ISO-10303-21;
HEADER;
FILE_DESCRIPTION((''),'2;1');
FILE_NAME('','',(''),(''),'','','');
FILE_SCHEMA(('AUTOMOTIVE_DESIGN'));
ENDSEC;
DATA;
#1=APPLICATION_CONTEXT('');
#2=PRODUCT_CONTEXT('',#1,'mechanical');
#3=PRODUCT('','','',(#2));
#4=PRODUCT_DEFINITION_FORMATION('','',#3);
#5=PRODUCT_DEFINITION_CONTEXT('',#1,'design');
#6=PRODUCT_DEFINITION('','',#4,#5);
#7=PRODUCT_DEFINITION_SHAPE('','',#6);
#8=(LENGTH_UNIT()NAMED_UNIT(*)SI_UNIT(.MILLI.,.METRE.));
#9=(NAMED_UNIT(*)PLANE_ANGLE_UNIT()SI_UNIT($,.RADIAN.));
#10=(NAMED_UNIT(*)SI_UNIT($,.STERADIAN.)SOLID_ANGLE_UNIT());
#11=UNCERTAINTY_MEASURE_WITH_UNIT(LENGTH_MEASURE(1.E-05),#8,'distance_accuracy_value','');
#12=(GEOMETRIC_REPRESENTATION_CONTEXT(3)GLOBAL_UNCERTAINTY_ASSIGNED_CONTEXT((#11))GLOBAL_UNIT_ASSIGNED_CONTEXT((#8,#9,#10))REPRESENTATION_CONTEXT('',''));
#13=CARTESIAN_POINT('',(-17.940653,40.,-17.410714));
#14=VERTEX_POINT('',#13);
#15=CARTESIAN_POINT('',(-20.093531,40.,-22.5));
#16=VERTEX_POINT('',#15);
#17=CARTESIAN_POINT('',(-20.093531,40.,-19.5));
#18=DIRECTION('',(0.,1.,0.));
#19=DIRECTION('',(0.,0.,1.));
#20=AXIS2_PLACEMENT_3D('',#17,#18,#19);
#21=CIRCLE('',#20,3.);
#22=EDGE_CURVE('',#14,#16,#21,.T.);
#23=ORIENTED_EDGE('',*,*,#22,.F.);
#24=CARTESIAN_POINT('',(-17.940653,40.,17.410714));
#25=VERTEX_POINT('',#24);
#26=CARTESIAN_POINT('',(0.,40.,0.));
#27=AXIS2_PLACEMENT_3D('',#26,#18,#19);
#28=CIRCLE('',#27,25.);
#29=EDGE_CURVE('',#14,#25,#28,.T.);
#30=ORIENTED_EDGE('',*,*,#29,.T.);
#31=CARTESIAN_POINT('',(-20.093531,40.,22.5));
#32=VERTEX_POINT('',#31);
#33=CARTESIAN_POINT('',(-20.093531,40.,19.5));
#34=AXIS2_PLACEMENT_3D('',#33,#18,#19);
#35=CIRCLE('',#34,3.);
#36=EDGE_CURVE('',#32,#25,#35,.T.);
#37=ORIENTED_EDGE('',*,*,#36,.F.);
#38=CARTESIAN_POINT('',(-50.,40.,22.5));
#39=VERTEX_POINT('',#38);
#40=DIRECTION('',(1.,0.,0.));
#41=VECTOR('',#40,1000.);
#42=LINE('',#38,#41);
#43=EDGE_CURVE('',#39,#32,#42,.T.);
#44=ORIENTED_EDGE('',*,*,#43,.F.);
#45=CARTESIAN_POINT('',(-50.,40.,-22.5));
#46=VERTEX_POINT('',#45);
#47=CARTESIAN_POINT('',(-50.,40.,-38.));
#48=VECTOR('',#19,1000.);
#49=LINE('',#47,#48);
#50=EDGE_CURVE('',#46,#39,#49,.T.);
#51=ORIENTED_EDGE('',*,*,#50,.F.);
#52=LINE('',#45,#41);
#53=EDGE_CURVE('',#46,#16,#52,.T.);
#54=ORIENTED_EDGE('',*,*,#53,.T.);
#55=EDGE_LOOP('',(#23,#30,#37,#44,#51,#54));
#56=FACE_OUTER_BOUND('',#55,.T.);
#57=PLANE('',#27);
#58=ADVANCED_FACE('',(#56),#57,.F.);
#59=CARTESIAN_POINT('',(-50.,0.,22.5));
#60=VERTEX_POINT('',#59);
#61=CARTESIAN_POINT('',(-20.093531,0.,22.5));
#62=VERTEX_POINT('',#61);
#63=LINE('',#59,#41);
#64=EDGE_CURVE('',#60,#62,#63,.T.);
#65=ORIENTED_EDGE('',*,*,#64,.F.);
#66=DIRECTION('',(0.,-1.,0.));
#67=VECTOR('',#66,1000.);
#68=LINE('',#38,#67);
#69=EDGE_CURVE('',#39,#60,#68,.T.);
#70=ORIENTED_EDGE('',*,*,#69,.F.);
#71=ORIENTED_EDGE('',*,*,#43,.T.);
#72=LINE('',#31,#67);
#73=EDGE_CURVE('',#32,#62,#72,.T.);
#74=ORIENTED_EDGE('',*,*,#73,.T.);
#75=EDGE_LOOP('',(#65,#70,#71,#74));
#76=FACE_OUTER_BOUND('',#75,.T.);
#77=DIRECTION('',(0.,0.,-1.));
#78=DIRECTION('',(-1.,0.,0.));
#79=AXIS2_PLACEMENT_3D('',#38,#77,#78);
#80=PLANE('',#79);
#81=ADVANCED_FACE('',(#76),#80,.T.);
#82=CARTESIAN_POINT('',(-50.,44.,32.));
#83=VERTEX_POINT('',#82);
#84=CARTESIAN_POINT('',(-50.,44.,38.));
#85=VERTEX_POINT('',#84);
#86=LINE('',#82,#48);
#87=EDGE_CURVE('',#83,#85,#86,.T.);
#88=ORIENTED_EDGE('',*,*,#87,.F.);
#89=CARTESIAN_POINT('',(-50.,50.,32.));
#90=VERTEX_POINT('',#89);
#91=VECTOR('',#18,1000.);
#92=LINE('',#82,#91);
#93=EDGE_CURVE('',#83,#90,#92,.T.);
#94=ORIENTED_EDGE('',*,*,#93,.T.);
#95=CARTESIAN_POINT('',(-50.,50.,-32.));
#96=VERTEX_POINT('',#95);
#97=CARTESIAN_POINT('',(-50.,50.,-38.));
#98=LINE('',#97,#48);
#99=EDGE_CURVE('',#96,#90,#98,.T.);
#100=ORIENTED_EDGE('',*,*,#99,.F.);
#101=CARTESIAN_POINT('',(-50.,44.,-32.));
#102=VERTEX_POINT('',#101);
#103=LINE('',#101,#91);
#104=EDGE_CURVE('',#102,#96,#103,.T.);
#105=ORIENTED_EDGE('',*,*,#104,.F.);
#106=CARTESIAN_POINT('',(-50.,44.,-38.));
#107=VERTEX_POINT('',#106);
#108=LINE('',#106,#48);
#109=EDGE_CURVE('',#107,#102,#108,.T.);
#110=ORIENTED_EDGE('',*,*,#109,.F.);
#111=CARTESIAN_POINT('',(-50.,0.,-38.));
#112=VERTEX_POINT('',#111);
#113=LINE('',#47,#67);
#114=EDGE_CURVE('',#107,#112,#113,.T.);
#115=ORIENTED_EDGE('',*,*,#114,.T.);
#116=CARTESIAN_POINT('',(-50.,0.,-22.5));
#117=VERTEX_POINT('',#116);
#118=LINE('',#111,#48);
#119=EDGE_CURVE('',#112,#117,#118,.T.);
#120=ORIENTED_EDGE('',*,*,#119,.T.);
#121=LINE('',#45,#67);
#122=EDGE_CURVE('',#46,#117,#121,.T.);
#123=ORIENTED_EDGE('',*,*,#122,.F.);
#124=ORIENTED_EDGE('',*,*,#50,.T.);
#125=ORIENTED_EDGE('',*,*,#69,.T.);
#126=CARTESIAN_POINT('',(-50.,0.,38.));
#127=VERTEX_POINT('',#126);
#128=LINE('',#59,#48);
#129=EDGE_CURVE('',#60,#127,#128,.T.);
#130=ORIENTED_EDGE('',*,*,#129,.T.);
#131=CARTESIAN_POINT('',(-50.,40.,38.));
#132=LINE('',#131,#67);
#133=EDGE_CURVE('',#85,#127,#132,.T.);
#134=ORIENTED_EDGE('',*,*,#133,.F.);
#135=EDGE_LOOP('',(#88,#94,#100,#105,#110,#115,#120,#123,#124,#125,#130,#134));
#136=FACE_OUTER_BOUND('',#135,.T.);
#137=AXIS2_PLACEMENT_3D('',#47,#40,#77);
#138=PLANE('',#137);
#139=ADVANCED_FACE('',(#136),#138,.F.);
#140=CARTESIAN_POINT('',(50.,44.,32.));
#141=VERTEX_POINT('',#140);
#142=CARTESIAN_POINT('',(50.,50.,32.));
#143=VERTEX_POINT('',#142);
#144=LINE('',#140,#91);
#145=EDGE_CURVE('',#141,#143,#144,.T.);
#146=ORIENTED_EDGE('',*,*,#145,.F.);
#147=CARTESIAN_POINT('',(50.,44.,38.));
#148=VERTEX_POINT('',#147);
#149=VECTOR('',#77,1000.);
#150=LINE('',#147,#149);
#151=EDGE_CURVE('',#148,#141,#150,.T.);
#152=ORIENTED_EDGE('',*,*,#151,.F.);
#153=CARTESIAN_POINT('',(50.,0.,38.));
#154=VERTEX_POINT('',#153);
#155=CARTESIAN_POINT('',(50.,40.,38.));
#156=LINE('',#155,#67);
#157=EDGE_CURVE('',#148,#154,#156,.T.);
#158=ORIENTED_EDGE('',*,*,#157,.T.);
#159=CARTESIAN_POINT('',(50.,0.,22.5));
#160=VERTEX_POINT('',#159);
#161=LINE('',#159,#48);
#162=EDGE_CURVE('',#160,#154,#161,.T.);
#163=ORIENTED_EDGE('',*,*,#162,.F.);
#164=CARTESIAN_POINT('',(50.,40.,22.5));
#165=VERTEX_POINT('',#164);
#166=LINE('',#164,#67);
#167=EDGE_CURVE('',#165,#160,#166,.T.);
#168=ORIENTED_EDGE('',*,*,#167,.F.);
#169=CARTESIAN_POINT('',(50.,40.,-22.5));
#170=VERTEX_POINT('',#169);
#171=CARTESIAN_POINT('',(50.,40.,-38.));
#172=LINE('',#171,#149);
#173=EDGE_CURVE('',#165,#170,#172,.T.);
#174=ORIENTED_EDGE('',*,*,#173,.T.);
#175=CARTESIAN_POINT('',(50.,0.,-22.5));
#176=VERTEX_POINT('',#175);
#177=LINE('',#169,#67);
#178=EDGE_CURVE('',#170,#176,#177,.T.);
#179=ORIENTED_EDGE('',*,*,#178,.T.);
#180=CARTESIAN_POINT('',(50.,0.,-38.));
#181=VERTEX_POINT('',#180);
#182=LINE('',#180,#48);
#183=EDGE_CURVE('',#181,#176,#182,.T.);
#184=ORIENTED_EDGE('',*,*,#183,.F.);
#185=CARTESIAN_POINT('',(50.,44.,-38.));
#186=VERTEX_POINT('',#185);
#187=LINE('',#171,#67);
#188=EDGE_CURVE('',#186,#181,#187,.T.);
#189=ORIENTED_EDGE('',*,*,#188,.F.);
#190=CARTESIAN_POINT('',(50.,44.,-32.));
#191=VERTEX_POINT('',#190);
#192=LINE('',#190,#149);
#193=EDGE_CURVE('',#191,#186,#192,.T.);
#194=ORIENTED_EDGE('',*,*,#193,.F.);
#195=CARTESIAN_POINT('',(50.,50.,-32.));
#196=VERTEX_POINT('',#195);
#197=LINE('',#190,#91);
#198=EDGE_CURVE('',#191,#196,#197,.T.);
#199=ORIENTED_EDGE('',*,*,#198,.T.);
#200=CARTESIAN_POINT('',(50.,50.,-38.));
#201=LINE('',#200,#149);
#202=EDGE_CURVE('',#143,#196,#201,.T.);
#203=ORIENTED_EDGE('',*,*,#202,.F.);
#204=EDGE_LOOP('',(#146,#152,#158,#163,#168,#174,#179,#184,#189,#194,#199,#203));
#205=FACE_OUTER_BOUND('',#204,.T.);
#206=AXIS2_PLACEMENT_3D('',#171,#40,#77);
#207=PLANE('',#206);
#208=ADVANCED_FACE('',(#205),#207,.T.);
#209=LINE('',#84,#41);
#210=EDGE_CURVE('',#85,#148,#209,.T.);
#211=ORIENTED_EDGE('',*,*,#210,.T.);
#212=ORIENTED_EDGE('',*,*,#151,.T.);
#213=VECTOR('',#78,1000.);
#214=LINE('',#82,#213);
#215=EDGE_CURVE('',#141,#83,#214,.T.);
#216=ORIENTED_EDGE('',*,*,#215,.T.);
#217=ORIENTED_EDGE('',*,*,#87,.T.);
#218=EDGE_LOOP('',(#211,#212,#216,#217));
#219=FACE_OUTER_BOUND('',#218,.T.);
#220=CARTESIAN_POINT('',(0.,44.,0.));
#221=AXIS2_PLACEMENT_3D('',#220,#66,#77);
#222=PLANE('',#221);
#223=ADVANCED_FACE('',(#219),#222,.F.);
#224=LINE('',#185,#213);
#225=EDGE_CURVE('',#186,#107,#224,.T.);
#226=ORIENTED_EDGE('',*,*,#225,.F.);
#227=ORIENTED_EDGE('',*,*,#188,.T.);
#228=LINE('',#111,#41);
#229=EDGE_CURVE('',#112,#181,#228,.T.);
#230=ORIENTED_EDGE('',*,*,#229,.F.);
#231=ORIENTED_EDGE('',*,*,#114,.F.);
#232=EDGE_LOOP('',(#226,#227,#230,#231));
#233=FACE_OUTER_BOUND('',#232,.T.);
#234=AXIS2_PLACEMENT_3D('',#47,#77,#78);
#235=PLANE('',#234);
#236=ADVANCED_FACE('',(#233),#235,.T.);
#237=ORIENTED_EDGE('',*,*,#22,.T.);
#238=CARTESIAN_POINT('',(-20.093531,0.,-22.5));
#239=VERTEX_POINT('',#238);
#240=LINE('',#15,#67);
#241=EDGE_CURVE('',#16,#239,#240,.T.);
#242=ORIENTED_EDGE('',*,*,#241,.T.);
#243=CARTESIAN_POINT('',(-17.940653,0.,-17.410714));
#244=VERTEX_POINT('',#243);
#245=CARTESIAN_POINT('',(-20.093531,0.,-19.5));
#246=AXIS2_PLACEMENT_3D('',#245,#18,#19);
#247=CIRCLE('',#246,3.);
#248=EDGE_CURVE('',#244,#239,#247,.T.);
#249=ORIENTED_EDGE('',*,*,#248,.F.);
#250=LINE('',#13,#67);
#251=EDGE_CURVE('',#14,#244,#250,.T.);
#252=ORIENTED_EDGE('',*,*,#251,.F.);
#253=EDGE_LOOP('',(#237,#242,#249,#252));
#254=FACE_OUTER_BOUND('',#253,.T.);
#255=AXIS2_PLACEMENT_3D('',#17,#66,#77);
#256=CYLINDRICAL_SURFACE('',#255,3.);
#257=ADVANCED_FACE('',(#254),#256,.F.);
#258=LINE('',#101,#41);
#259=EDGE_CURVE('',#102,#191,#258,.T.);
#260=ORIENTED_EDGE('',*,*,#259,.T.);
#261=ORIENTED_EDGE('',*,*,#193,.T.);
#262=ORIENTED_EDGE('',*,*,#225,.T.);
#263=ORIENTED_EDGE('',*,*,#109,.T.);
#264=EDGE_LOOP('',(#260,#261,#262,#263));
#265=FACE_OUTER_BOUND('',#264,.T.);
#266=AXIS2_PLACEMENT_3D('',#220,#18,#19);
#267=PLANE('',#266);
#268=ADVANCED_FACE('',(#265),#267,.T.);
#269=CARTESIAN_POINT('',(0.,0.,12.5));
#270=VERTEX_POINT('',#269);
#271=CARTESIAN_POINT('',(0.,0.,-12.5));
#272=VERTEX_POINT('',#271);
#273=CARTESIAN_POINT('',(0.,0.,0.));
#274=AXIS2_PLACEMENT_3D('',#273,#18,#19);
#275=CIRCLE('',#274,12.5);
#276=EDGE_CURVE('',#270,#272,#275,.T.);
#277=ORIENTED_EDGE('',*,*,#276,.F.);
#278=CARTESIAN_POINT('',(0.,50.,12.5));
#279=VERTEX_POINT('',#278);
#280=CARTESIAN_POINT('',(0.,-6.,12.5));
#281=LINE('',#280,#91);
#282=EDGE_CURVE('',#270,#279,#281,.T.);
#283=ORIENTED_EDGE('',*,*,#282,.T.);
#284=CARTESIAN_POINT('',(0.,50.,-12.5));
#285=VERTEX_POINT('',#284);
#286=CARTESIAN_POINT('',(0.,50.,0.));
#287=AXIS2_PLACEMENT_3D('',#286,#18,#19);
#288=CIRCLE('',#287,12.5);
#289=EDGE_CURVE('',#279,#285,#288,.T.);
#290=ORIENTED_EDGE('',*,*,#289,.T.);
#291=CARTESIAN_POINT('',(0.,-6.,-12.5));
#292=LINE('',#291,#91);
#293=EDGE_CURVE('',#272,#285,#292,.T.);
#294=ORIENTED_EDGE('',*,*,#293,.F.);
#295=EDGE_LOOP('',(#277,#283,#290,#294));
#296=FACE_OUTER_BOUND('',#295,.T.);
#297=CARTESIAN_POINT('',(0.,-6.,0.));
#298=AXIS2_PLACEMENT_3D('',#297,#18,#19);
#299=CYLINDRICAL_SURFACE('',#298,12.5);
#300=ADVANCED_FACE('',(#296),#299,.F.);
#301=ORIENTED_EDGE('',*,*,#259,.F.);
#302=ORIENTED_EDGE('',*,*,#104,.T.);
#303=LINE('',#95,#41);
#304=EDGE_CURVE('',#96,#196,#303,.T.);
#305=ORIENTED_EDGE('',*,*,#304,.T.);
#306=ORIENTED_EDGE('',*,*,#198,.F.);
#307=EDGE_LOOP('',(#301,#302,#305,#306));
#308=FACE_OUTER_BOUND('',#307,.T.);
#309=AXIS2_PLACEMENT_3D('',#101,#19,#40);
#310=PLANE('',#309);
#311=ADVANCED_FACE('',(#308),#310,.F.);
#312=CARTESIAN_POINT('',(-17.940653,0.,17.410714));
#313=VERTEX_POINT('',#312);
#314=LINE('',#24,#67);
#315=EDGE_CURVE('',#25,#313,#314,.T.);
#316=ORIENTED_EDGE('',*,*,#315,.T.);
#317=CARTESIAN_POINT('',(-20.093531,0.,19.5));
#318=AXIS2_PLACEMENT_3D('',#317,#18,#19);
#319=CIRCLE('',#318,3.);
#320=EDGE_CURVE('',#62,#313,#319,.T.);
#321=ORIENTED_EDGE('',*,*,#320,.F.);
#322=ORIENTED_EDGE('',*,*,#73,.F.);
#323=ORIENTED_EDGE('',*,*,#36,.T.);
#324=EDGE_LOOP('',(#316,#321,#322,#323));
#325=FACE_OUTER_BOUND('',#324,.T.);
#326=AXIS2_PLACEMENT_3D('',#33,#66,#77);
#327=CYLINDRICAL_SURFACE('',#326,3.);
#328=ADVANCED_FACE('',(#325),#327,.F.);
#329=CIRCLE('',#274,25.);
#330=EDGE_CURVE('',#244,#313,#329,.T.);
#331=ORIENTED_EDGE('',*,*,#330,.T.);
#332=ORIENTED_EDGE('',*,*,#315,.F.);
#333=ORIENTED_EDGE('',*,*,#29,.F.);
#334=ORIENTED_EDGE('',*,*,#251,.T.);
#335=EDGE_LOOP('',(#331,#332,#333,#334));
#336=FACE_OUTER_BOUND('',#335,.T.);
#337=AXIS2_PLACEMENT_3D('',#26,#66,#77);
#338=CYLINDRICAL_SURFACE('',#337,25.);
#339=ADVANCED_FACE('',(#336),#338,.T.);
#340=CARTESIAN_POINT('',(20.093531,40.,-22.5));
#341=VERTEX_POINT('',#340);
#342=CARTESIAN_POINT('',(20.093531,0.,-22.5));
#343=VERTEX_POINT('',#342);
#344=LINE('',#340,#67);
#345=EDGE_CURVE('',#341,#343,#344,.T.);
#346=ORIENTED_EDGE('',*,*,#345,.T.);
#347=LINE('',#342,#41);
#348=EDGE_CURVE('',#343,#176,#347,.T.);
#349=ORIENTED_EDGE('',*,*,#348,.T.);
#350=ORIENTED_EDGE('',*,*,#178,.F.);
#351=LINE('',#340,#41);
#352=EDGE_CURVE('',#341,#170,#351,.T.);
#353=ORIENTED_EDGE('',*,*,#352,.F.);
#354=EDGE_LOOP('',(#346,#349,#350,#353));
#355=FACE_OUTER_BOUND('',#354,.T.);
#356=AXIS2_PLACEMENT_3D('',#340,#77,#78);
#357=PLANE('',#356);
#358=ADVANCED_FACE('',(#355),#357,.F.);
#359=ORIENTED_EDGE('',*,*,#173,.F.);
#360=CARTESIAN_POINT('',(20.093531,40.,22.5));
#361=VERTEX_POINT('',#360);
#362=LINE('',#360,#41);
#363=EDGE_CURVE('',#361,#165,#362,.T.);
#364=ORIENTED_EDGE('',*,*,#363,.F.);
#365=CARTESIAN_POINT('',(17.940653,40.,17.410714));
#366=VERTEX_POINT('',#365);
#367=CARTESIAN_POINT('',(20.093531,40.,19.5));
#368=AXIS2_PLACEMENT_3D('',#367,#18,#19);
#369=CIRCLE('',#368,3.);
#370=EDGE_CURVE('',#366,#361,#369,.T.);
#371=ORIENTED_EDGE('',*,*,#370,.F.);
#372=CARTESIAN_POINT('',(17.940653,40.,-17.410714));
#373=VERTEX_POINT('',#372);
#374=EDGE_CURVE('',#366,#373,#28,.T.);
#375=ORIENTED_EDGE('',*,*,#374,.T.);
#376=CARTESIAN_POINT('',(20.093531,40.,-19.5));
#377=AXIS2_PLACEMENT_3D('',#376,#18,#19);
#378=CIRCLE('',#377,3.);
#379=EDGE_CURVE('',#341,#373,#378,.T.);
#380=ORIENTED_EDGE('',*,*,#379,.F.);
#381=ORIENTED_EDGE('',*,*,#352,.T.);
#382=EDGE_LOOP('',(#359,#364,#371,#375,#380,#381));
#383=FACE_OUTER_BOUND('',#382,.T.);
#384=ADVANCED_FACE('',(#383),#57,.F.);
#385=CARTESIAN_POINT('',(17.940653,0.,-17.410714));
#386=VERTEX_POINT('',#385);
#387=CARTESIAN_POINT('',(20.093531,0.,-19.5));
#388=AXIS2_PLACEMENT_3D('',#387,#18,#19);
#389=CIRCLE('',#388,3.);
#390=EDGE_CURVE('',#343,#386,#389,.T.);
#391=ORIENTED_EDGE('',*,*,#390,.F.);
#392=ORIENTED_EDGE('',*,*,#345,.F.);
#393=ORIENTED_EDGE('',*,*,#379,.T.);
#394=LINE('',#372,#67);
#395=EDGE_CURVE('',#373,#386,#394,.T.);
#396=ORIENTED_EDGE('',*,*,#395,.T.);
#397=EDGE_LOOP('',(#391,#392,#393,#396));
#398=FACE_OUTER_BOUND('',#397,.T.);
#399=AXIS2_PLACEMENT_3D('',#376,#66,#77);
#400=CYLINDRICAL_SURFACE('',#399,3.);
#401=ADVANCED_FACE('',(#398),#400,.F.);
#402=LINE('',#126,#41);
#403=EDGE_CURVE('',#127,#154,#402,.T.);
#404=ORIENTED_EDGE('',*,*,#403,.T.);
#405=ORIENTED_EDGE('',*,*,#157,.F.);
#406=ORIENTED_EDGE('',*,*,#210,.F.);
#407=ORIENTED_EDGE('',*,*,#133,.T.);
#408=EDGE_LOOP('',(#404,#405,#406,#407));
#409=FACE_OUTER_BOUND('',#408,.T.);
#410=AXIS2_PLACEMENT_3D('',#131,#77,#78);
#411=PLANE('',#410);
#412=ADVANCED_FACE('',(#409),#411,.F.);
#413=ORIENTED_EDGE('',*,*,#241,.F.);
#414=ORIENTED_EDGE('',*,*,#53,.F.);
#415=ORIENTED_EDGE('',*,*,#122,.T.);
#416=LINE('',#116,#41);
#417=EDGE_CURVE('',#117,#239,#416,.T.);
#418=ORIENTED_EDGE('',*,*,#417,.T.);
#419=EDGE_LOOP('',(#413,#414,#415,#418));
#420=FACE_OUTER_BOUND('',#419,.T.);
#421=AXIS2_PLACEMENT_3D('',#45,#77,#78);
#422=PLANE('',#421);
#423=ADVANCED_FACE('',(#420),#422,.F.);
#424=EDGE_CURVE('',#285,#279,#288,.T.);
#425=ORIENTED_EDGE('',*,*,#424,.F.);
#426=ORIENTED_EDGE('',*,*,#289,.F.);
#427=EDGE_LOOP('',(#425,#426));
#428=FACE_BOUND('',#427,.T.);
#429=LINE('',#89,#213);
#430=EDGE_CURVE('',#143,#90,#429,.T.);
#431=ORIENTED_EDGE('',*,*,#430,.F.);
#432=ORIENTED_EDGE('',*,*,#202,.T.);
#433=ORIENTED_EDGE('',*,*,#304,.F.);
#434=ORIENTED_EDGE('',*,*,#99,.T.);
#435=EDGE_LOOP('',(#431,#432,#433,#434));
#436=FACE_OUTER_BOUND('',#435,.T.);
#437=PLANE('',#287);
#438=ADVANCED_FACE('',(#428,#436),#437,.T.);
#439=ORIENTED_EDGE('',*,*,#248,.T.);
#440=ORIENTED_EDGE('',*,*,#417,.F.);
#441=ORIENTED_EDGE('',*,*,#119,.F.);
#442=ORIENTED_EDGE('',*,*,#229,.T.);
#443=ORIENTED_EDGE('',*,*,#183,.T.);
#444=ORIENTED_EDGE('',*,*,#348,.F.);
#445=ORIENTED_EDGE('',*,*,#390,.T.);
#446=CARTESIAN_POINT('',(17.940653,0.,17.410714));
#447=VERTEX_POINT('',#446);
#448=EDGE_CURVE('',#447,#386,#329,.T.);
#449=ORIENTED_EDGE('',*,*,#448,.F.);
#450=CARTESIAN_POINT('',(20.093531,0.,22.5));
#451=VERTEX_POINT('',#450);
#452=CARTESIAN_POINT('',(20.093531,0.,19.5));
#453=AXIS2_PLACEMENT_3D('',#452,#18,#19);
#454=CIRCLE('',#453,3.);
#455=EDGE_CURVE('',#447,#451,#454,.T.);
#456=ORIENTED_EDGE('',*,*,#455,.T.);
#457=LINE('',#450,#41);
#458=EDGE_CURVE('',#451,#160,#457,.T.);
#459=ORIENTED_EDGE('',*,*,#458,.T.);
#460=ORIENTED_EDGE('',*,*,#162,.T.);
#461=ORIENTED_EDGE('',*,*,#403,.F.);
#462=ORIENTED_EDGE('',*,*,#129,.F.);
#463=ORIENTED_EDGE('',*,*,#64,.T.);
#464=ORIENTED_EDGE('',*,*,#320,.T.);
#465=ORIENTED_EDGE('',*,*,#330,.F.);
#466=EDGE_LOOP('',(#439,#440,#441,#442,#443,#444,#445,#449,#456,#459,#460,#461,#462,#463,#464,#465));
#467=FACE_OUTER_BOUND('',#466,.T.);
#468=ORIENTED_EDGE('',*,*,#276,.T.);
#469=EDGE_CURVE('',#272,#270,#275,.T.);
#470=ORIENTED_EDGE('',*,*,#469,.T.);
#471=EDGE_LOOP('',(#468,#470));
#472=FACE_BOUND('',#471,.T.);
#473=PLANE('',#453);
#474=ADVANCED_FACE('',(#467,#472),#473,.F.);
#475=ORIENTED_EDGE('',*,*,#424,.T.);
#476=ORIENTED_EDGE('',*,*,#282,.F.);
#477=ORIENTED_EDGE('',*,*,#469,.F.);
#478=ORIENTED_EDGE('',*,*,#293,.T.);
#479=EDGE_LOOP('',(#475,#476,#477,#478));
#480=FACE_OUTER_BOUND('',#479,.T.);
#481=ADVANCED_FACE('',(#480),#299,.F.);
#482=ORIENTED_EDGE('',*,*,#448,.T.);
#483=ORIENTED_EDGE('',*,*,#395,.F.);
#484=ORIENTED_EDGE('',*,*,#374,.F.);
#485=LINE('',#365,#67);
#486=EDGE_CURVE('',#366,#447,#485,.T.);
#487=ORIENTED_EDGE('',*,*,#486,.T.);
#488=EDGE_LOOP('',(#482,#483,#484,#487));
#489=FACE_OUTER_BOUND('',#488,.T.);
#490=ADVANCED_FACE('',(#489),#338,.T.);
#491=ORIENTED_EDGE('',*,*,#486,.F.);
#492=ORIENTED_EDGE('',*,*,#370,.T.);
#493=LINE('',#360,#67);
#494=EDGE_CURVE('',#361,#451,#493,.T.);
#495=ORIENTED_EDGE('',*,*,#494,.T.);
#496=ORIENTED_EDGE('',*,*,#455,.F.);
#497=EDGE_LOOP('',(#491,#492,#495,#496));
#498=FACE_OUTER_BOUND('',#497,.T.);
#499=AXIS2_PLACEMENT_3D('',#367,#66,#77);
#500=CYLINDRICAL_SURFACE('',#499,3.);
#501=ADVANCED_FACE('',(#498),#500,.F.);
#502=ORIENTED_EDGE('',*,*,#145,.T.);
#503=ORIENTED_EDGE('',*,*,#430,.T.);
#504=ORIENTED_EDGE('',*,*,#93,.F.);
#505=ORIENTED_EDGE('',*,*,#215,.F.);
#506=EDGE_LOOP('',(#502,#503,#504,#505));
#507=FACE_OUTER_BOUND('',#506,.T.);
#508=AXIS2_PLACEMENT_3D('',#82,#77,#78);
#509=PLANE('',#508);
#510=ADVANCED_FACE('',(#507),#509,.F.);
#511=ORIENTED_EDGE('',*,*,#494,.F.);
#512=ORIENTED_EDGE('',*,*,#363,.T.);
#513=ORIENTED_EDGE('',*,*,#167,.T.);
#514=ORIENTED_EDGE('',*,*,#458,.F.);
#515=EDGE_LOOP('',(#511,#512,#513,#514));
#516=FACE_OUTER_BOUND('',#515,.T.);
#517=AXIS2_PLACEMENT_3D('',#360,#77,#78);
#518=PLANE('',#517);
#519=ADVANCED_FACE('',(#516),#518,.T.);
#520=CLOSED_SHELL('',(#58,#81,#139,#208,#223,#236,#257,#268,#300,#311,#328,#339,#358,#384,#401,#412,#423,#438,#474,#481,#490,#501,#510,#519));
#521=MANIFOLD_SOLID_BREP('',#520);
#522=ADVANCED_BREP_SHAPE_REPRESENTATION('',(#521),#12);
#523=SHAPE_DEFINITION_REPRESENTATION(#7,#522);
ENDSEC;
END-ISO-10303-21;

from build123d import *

# Parameters (mm, degrees)
CHANNEL_BODY_DEPTH      = 40
TOP_PLATE_SKETCH_W      = 100
TOP_PLATE_SKETCH_H      = 76
TOP_PLATE_DEPTH         = 10
BORE_SKETCH_R           = 12.5
BORE_25_DEPTH           = 56
GUIDE_GROOVES_SKETCH_W  = 100
GUIDE_GROOVES_SKETCH_H  = 6
GUIDE_GROOVES_6X6_DEPTH = 6


with BuildPart() as part:
    # Channel Profile Sketch → Channel Body (new body)
    with BuildSketch(Plane(origin=(0, 0, 0), x_dir=(1, 0, 0), z_dir=(0, 1, 0))):
        with BuildLine():
            Line((-50, 22.5), (-20.093531297, 22.5))
            ThreePointArc((-20.093531297, 22.5), (-17.330574806, 20.668790584), (-17.940652944, 17.410714286))
            ThreePointArc((-17.940652944, 17.410714286), (-25, 0), (-17.940652944, -17.410714286))
            ThreePointArc((-17.940652944, -17.410714286), (-17.330574806, -20.668790584), (-20.093531297, -22.5))
            Line((-20.093531297, -22.5), (-50, -22.5))
            Line((-50, -22.5), (-50, -38))
            Line((-50, -38), (50, -38))
            Line((50, -38), (50, -22.5))
            Line((50, -22.5), (20.093531297, -22.5))
            ThreePointArc((20.093531297, -22.5), (17.330574806, -20.668790584), (17.940652944, -17.410714286))
            ThreePointArc((17.940652944, -17.410714286), (25, 0), (17.940652944, 17.410714286))
            ThreePointArc((17.940652944, 17.410714286), (17.330574806, 20.668790584), (20.093531297, 22.5))
            Line((20.093531297, 22.5), (50, 22.5))
            Line((50, 22.5), (50, 38))
            Line((50, 38), (-50, 38))
            Line((-50, 38), (-50, 22.5))
        make_face()
    extrude(amount=CHANNEL_BODY_DEPTH)

    # Top Plate Sketch → Top Plate (add)
    with BuildSketch(Plane(origin=(0, 40, 0), x_dir=(1, 0, 0), z_dir=(0, 1, 0))):
        Rectangle(TOP_PLATE_SKETCH_W, TOP_PLATE_SKETCH_H)
    extrude(amount=TOP_PLATE_DEPTH)

    # Bore Sketch → Bore Ø25 (cut)
    with BuildSketch(Plane(origin=(0, 50, 0), x_dir=(1, 0, 0), z_dir=(0, 1, 0))):
        with Locations(Location((0, 0, 0), (0, 0, 270))):
            Circle(BORE_SKETCH_R)
    extrude(amount=-BORE_25_DEPTH, mode=Mode.SUBTRACT)

    # Guide Grooves Sketch → Guide Grooves 6x6 (cut)
    with BuildSketch(Plane(origin=(0, 50, 0), x_dir=(1, 0, 0), z_dir=(0, 1, 0))):
        with Locations((0, 35)):
            Rectangle(GUIDE_GROOVES_SKETCH_W, GUIDE_GROOVES_SKETCH_H)
        with Locations((0, -35)):
            Rectangle(GUIDE_GROOVES_SKETCH_W, GUIDE_GROOVES_SKETCH_H)
    extrude(amount=-GUIDE_GROOVES_6X6_DEPTH, mode=Mode.SUBTRACT)


solid = part.part
